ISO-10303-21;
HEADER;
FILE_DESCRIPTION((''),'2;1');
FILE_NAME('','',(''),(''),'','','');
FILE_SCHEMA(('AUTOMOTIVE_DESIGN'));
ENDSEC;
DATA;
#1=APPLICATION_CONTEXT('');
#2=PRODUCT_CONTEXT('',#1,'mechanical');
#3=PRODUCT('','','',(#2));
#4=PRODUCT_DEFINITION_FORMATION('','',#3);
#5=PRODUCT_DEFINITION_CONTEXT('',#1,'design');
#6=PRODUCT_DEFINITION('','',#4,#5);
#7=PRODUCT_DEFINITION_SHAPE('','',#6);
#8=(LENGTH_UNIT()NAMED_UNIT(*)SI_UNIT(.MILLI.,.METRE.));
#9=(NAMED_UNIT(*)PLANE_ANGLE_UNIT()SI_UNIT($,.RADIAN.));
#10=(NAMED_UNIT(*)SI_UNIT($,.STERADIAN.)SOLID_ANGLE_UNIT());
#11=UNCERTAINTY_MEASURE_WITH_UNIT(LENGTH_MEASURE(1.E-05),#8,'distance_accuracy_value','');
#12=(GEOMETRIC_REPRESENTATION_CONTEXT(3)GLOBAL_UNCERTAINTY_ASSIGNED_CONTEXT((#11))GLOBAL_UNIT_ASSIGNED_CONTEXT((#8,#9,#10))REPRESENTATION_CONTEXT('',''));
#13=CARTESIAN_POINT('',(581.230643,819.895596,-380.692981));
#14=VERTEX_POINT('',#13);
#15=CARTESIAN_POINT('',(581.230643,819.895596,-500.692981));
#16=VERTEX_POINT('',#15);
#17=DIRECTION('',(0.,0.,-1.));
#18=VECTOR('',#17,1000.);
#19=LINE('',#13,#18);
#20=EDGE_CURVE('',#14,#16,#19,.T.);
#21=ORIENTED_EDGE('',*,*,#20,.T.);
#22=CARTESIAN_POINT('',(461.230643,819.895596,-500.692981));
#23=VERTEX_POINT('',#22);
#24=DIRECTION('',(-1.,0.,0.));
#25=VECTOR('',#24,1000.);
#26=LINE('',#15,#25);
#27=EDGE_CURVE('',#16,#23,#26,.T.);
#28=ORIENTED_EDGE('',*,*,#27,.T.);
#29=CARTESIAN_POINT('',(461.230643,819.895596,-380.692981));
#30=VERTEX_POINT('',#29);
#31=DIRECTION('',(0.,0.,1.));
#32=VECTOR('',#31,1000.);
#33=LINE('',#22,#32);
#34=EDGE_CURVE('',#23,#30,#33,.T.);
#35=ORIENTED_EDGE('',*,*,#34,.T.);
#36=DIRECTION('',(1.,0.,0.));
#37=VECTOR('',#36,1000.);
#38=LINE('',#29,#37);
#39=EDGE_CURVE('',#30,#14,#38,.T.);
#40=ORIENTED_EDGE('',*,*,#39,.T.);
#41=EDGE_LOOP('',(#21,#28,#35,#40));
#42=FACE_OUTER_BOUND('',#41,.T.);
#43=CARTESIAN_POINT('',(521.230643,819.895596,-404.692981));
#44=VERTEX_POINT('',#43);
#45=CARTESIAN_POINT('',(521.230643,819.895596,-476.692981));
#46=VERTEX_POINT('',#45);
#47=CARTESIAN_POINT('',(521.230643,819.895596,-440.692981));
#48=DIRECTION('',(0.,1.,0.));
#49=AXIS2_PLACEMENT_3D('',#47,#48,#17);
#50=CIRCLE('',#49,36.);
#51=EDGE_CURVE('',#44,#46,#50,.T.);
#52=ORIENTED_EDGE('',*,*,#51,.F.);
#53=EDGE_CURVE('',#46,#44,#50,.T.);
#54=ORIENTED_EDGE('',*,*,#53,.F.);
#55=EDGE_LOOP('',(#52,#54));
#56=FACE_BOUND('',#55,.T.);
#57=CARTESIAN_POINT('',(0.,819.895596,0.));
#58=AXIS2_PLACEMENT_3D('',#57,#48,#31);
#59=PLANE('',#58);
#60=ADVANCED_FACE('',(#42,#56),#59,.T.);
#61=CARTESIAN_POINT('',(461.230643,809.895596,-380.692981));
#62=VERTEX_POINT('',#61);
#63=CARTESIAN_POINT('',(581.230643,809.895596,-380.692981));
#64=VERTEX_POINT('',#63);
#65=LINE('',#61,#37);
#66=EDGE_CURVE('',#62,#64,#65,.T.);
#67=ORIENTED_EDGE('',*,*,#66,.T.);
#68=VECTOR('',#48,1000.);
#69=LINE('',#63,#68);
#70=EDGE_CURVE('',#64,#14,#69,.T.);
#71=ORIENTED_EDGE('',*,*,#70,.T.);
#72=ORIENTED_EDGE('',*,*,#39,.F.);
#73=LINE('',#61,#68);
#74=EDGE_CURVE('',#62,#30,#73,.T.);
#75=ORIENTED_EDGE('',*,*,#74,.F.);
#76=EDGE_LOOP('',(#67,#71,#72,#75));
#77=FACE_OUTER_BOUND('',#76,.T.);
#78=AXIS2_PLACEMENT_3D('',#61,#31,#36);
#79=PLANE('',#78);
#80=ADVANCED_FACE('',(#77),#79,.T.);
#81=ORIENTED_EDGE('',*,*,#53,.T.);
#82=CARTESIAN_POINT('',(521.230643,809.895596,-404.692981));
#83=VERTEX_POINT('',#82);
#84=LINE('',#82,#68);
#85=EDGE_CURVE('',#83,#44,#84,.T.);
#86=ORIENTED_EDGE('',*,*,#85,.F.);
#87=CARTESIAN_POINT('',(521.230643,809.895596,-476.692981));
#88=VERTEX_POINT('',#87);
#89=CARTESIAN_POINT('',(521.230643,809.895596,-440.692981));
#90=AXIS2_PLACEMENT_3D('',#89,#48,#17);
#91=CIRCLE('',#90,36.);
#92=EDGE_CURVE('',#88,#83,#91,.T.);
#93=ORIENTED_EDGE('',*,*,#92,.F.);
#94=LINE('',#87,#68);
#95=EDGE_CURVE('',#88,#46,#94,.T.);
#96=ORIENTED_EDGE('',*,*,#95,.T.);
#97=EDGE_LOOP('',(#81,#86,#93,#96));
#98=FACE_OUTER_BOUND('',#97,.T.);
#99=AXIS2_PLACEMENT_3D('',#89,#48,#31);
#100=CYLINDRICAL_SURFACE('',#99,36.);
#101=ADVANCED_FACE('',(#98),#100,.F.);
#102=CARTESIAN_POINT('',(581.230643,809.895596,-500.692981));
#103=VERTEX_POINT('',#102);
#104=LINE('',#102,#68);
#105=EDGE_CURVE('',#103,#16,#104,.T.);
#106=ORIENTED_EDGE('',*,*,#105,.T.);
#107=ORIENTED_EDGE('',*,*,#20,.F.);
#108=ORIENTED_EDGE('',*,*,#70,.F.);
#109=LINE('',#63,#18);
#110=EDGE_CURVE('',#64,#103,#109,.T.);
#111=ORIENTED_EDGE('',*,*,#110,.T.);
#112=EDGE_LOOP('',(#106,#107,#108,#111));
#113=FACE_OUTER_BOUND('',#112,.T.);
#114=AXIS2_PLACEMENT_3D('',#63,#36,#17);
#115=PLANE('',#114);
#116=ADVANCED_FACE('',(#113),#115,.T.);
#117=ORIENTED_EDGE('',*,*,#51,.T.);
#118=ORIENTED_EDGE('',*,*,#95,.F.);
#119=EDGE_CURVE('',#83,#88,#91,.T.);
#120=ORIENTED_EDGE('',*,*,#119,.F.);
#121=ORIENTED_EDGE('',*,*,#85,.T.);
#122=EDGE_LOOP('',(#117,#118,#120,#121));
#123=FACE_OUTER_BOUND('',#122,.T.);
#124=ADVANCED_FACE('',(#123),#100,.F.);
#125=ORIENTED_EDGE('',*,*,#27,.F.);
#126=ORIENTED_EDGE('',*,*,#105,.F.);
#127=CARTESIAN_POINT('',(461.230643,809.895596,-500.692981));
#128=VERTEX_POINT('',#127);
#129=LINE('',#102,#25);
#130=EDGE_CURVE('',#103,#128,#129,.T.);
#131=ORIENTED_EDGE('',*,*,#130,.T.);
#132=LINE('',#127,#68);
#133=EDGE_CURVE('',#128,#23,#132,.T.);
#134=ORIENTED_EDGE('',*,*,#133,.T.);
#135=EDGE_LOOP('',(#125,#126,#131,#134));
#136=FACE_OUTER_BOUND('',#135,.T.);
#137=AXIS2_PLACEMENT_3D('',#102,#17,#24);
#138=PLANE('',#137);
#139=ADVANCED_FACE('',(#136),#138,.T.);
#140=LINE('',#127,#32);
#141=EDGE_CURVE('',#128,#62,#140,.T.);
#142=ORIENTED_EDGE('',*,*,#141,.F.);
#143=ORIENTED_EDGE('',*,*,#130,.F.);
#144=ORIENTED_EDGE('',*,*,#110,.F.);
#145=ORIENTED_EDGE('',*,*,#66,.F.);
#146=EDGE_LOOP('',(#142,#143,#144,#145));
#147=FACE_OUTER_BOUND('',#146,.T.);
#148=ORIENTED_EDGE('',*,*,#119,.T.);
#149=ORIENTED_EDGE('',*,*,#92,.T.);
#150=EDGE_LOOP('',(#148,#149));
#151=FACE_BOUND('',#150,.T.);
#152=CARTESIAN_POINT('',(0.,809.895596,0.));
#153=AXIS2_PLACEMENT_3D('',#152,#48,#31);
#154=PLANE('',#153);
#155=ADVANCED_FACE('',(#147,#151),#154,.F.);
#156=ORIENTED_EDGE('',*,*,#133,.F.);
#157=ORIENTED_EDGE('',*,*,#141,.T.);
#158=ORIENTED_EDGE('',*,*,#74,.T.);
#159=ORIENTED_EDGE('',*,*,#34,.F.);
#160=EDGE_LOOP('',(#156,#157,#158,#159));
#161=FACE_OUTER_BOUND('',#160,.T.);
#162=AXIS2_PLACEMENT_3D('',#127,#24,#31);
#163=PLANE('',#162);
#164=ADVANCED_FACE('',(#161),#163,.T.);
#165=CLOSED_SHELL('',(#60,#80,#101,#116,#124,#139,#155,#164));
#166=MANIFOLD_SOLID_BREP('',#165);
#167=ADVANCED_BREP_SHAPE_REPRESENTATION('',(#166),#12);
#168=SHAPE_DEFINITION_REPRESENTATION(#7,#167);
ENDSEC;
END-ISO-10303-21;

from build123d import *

# Parameters (mm, degrees)
SKETCH1_W           = 120
SKETCH1_H           = 120
SKETCH1_R           = 36
BOSS_EXTRUDE1_DEPTH = 10


with BuildPart() as part:
    # Sketch1 → Boss-Extrude1 (new body)
    with BuildSketch(Plane(origin=(0, 819.895595987, 0), x_dir=(1, 0, 0), z_dir=(0, 1, 0))):
        with Locations((521.230642584, 440.692981355)):
            Rectangle(SKETCH1_W, SKETCH1_H)
        with Locations(Location((521.230642584, 440.692981355, 0), (0, 0, 90))):
            Circle(SKETCH1_R, mode=Mode.SUBTRACT)
    extrude(amount=-BOSS_EXTRUDE1_DEPTH)


solid = part.part
